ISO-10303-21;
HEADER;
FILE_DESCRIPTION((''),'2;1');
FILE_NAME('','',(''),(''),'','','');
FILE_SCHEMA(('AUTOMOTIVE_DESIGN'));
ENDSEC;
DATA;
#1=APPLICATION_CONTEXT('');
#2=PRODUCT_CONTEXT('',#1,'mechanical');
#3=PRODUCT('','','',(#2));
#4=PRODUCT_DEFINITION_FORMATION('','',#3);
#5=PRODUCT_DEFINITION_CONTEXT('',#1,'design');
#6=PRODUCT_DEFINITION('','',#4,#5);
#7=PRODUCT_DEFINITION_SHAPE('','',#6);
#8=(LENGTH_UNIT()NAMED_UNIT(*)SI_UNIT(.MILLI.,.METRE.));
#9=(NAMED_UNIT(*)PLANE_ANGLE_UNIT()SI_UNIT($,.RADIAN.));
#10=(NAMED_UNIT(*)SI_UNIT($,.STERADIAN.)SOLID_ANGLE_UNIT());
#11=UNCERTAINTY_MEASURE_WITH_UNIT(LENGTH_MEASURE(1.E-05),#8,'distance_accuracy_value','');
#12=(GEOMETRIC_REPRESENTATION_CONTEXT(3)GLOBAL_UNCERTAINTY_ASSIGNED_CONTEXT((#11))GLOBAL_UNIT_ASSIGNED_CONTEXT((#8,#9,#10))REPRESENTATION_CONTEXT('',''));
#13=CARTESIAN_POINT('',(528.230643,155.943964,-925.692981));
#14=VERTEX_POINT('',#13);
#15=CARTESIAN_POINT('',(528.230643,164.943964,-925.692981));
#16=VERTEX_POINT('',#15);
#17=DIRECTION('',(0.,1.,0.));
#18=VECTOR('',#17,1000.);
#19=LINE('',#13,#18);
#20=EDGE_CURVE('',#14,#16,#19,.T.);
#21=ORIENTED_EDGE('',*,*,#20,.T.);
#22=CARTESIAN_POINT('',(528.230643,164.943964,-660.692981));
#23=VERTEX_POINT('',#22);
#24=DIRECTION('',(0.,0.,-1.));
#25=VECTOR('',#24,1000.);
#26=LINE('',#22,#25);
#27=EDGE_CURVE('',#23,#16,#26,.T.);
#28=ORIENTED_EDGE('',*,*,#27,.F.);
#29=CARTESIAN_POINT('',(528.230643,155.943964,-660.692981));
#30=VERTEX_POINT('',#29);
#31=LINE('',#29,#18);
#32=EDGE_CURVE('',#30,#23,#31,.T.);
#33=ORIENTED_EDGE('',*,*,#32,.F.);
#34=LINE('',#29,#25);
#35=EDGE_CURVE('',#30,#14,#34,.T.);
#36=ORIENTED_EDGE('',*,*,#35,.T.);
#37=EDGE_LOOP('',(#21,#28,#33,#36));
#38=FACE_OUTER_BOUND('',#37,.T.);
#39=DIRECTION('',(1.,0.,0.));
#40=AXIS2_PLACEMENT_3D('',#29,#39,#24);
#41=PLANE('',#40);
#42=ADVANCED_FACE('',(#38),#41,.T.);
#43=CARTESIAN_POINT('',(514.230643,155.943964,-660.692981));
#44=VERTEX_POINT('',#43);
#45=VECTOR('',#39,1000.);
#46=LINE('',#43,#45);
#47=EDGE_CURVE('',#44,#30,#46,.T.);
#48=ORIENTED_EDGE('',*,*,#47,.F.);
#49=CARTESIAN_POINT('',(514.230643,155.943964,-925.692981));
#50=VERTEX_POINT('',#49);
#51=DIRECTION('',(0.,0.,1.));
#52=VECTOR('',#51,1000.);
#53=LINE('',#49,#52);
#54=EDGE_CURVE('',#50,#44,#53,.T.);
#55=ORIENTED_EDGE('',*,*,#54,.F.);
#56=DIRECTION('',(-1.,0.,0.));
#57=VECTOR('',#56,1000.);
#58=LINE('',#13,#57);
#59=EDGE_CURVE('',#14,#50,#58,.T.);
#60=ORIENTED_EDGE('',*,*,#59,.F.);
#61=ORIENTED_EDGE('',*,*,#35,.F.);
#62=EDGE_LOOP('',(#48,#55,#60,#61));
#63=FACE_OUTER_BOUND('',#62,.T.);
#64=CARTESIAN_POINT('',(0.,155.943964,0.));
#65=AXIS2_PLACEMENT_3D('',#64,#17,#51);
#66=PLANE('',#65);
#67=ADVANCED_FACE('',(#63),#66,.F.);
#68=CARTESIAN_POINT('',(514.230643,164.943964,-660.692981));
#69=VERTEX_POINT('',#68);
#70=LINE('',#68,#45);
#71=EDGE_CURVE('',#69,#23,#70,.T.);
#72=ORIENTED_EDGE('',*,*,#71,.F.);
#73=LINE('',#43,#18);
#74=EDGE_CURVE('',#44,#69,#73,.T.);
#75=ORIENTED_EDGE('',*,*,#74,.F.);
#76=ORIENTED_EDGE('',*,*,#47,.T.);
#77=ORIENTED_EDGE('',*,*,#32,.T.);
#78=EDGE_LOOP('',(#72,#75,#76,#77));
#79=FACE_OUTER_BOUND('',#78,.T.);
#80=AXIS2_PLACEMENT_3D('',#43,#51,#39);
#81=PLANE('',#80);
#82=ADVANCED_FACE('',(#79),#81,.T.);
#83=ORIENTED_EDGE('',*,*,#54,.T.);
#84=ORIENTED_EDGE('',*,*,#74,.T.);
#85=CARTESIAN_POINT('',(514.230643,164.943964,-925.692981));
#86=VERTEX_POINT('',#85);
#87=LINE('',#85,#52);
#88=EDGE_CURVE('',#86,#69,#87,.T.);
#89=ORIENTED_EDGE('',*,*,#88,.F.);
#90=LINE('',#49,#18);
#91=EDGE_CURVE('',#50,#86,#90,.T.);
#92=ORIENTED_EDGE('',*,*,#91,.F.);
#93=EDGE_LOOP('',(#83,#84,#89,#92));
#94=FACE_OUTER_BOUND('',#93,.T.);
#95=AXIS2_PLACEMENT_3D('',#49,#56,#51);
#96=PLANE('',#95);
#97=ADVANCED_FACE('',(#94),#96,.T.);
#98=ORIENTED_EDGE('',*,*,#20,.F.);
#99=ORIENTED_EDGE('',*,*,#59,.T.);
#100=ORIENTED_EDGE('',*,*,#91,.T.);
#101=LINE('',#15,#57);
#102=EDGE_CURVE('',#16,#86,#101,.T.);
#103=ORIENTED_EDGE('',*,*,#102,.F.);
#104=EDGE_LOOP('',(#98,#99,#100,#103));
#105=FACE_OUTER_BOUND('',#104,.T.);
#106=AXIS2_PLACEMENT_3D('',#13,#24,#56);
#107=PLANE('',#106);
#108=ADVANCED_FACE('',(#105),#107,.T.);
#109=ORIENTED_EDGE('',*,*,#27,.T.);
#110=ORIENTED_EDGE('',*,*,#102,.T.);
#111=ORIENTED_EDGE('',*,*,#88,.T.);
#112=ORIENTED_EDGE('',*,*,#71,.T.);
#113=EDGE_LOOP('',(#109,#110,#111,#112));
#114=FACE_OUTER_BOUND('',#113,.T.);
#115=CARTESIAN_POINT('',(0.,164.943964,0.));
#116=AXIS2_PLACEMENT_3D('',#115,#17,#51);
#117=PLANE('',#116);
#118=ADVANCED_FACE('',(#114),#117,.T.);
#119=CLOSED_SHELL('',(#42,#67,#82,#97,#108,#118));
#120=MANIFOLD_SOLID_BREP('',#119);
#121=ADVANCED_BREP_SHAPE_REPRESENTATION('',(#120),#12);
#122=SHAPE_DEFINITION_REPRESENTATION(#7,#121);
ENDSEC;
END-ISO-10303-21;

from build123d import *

# Parameters (mm, degrees)
SKETCH1_W           = 14
SKETCH1_H           = 265
BOSS_EXTRUDE1_DEPTH = 9


with BuildPart() as part:
    # Sketch1 → Boss-Extrude1 (new body)
    with BuildSketch(Plane(origin=(0, 164.943963655, 0), x_dir=(1, 0, 0), z_dir=(0, 1, 0))):
        with Locations((521.230642584, 793.192981355)):
            Rectangle(SKETCH1_W, SKETCH1_H)
    extrude(amount=-BOSS_EXTRUDE1_DEPTH)


solid = part.part
